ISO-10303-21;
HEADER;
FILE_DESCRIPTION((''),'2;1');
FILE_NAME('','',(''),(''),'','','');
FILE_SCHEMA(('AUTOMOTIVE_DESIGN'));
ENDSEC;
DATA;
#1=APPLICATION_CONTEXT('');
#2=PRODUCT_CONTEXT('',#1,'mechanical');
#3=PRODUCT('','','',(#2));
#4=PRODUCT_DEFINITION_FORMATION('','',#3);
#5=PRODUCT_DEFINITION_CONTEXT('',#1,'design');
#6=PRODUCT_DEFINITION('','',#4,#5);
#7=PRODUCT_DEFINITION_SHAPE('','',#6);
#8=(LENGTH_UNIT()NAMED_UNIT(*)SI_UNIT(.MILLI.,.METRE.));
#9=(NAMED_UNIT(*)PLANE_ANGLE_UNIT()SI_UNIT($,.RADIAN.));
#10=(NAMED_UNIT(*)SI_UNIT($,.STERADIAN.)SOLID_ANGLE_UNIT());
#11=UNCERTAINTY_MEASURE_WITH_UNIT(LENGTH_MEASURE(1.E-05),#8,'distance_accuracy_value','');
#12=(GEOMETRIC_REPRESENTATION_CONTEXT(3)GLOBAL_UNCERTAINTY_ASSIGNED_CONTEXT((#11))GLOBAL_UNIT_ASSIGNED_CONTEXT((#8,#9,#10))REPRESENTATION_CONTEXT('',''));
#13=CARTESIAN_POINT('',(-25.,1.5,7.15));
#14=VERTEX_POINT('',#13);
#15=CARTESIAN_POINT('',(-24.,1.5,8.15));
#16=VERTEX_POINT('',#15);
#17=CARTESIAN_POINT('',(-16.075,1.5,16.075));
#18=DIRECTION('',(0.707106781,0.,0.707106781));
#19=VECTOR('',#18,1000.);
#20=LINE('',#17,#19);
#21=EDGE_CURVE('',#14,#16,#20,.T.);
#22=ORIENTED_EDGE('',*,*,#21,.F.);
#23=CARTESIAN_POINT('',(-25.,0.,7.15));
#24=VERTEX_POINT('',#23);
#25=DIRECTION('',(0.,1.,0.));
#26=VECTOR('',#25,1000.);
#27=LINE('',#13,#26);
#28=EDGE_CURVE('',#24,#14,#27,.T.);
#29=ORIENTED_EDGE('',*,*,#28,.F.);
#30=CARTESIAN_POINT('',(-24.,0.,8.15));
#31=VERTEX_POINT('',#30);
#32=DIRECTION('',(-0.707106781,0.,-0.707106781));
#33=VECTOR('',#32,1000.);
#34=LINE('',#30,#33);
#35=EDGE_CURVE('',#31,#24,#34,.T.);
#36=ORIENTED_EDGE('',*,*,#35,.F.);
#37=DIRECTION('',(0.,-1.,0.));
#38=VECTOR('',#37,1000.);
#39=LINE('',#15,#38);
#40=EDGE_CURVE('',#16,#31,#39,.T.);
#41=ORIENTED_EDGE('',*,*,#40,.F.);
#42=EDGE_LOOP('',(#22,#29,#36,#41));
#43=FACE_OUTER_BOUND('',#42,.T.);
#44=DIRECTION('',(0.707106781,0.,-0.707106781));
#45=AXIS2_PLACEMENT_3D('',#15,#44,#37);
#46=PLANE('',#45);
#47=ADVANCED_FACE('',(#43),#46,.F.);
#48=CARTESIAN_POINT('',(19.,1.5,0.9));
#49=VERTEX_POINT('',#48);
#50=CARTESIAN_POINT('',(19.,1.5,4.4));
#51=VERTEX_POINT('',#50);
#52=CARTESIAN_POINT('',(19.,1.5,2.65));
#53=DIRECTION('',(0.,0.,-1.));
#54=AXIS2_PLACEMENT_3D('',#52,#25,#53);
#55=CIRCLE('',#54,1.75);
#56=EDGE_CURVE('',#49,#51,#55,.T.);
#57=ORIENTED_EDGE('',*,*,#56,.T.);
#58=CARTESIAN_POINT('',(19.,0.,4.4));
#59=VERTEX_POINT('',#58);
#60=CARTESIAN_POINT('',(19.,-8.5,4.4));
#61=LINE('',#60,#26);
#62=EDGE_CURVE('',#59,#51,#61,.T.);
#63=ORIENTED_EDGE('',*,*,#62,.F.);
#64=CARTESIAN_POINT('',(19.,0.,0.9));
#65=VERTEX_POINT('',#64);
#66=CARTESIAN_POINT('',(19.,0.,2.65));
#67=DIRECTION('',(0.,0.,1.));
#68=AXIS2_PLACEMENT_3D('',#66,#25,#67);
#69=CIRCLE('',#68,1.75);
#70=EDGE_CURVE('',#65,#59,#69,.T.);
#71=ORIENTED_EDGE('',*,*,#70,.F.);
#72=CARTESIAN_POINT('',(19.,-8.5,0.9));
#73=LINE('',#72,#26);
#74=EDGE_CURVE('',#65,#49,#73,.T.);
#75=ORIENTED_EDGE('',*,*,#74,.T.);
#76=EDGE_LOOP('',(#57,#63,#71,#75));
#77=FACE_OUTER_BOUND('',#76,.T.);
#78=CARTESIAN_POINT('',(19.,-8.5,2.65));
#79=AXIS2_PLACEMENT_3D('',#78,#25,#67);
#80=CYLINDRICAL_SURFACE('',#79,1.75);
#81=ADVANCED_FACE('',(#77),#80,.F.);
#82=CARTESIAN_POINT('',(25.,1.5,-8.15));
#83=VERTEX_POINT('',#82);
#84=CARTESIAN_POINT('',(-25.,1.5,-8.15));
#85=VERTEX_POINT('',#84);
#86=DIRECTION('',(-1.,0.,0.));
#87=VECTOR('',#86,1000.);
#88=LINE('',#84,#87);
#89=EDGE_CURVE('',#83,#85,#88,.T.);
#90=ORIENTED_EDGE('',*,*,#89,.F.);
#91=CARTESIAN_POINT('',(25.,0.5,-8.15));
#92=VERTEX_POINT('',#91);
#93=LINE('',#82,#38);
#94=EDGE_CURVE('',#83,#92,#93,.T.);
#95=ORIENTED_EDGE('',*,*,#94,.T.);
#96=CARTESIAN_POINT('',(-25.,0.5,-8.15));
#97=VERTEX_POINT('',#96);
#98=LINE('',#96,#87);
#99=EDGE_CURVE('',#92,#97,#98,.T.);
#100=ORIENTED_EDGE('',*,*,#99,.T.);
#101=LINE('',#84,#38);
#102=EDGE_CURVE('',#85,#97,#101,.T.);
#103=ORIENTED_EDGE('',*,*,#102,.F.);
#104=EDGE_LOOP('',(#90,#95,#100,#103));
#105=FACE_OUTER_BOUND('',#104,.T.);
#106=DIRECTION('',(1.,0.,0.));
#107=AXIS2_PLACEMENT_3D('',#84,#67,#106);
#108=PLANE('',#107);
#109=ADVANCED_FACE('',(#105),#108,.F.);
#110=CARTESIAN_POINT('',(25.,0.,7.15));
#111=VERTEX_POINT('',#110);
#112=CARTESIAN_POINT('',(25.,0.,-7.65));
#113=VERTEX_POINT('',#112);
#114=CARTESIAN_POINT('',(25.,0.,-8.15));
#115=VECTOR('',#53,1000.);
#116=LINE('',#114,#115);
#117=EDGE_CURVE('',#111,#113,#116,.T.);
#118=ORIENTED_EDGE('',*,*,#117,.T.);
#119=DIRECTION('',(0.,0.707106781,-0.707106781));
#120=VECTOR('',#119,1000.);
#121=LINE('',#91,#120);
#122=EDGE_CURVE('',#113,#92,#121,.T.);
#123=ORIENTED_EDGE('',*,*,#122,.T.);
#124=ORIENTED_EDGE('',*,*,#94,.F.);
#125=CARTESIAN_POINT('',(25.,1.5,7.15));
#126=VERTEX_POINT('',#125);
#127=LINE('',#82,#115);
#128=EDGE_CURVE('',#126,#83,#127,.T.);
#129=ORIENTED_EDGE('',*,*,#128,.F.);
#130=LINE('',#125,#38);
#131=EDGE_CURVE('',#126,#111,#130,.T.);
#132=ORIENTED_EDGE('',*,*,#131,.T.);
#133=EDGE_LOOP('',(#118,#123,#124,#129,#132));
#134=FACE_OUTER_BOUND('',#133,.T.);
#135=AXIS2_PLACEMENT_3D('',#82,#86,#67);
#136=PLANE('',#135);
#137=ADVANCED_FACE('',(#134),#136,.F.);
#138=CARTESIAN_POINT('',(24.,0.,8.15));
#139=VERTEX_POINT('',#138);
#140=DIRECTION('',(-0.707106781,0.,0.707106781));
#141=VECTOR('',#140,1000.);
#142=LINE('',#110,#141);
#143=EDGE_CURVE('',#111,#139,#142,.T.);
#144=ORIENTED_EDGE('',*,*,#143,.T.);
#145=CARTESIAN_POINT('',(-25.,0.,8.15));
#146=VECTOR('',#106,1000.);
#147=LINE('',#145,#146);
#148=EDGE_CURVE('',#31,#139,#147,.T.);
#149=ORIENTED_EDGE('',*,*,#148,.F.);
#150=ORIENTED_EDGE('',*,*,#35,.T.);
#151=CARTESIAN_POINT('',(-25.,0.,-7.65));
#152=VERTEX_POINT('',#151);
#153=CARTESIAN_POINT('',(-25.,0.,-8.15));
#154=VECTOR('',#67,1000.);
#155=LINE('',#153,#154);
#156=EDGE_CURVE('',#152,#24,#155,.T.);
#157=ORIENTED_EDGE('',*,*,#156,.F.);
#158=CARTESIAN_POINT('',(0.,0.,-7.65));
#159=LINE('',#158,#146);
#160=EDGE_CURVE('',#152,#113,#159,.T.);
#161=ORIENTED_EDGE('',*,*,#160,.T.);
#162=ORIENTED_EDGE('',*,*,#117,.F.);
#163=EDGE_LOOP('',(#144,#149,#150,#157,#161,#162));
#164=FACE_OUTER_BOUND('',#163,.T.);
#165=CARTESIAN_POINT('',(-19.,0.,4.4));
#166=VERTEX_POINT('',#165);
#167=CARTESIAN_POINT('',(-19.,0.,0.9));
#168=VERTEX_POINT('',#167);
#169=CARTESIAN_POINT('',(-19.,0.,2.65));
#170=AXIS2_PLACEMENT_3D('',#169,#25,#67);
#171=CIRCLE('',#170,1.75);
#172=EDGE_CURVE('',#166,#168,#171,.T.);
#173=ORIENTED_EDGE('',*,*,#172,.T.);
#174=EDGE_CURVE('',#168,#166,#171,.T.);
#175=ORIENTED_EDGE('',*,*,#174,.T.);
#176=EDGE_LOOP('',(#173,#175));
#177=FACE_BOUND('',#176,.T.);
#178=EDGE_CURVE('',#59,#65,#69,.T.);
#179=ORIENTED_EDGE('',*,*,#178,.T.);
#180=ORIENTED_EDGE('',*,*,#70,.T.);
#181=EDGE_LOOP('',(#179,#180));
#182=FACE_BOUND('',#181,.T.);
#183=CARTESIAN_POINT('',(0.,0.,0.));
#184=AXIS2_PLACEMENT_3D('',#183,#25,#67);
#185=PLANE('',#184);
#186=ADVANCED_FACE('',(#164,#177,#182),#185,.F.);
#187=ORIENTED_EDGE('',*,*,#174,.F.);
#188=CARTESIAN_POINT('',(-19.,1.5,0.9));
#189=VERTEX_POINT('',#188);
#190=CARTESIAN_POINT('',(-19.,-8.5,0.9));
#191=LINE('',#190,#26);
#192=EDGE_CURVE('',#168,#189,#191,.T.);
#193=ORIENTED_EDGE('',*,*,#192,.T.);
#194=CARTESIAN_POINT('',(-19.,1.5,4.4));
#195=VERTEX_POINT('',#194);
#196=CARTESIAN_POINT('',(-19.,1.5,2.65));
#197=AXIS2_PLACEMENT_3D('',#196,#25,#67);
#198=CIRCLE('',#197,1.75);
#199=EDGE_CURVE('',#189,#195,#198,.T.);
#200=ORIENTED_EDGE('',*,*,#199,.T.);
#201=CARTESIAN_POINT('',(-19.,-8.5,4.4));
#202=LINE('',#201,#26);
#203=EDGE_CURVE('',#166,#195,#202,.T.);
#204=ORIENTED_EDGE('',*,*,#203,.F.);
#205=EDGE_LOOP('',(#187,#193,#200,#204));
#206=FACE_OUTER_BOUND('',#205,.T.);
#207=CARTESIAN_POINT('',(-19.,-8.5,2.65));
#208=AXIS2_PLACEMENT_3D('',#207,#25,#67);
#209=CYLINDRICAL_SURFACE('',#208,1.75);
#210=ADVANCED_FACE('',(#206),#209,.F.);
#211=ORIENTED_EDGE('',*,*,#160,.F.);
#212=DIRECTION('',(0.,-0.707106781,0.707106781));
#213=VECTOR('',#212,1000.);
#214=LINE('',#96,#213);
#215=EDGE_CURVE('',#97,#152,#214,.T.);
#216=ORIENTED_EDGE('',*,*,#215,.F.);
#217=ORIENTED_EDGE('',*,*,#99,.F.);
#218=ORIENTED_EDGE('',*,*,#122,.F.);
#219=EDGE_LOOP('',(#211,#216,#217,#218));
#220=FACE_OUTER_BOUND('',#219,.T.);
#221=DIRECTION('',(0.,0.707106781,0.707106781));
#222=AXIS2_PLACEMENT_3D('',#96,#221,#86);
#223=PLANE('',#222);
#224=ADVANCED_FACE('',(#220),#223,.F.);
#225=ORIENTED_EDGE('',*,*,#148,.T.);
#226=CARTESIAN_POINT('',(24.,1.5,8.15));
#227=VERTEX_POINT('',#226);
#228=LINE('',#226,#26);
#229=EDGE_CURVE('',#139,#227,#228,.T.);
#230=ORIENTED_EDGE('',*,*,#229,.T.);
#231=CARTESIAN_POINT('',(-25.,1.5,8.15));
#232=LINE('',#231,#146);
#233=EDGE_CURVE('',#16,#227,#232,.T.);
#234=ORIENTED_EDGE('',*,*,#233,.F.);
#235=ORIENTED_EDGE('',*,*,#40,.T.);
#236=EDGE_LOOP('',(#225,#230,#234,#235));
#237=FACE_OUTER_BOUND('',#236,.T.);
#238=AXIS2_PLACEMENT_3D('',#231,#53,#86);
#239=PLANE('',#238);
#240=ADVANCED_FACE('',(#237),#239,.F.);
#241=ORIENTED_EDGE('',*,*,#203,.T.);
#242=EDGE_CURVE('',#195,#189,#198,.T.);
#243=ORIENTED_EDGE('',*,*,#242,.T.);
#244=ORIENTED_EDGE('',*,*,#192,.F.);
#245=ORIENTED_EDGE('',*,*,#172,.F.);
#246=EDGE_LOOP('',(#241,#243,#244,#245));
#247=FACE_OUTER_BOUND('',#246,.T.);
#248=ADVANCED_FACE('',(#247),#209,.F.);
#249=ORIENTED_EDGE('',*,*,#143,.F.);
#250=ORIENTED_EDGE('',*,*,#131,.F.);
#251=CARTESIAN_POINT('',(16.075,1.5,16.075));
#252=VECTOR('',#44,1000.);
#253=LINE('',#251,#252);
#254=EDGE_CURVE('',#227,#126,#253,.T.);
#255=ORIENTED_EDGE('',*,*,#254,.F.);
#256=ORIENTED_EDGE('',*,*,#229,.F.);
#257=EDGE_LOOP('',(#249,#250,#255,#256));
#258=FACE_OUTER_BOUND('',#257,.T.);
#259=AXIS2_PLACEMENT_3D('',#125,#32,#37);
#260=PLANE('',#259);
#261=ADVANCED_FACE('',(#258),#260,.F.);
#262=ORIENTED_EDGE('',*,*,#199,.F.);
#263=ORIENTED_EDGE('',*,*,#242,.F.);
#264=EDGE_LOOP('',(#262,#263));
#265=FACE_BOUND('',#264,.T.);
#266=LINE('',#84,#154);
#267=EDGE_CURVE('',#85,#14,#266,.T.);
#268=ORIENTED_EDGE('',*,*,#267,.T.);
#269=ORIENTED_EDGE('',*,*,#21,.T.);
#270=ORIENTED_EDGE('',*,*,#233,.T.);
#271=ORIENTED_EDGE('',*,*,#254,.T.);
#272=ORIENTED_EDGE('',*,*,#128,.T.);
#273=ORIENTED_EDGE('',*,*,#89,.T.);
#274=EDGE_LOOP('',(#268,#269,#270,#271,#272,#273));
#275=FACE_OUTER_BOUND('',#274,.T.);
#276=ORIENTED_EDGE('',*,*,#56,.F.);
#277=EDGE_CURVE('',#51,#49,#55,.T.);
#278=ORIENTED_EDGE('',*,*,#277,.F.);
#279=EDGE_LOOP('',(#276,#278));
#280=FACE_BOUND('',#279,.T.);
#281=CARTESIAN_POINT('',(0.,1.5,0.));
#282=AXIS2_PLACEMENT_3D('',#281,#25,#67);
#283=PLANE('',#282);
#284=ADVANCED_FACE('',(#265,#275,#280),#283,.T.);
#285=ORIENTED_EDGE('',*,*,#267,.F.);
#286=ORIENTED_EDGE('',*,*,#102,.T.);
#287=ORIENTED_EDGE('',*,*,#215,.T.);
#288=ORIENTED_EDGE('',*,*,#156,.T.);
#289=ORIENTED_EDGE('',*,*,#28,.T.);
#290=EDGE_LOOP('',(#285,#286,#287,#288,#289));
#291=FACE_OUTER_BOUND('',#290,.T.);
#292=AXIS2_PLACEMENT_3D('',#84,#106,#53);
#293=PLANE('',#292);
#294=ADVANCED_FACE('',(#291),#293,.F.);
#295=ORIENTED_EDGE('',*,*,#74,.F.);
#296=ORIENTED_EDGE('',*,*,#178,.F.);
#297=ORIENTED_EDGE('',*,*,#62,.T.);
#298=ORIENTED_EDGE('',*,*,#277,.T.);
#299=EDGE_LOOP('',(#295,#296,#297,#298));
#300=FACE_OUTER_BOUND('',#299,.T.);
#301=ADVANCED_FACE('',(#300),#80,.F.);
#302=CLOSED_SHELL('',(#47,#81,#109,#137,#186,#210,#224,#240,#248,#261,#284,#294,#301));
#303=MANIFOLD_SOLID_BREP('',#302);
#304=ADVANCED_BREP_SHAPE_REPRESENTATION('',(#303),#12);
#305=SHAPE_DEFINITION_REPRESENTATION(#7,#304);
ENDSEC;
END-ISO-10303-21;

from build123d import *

# Parameters (mm, degrees)
SKETCH1_W           = 50
SKETCH1_H           = 16.3
BOSS_EXTRUDE1_DEPTH = 1.5
SKETCH3_R           = 1.75
CUT_EXTRUDE2_DEPTH  = 10
CHAMFER1_SIZE       = 1
CHAMFER2_SIZE       = 0.5


with BuildPart() as part:
    # Sketch1 → Boss-Extrude1 (new body)
    with BuildSketch(Plane(origin=(0, 0, 0), x_dir=(1, 0, 0), z_dir=(0, 1, 0))):
        Rectangle(SKETCH1_W, SKETCH1_H)
    extrude(amount=BOSS_EXTRUDE1_DEPTH)

    # Sketch3 → Cut-Extrude2 (cut)
    with BuildSketch(Plane(origin=(0, 1.5, 0), x_dir=(1, 0, 0), z_dir=(0, 1, 0))):
        with Locations(Location((-19, -2.65, 0), (0, 0, 270))):
            Circle(SKETCH3_R)
        with Locations(Location((19, -2.65, 0), (0, 0, 270))):
            Circle(SKETCH3_R)
    extrude(amount=-CUT_EXTRUDE2_DEPTH, mode=Mode.SUBTRACT)

    # Chamfer1
    chamfer1_edges = [part.edges().sort_by_distance(p)[0] for p in [
        (25, 0.75, 8.15),
        (-25, 0.75, 8.15),
    ]]
    chamfer(chamfer1_edges, length=CHAMFER1_SIZE)

    # Chamfer2
    chamfer2_edges = [part.edges().sort_by_distance(p)[0] for p in [
        (0, 0, -8.15),
    ]]
    chamfer(chamfer2_edges, length=CHAMFER2_SIZE)


solid = part.part
